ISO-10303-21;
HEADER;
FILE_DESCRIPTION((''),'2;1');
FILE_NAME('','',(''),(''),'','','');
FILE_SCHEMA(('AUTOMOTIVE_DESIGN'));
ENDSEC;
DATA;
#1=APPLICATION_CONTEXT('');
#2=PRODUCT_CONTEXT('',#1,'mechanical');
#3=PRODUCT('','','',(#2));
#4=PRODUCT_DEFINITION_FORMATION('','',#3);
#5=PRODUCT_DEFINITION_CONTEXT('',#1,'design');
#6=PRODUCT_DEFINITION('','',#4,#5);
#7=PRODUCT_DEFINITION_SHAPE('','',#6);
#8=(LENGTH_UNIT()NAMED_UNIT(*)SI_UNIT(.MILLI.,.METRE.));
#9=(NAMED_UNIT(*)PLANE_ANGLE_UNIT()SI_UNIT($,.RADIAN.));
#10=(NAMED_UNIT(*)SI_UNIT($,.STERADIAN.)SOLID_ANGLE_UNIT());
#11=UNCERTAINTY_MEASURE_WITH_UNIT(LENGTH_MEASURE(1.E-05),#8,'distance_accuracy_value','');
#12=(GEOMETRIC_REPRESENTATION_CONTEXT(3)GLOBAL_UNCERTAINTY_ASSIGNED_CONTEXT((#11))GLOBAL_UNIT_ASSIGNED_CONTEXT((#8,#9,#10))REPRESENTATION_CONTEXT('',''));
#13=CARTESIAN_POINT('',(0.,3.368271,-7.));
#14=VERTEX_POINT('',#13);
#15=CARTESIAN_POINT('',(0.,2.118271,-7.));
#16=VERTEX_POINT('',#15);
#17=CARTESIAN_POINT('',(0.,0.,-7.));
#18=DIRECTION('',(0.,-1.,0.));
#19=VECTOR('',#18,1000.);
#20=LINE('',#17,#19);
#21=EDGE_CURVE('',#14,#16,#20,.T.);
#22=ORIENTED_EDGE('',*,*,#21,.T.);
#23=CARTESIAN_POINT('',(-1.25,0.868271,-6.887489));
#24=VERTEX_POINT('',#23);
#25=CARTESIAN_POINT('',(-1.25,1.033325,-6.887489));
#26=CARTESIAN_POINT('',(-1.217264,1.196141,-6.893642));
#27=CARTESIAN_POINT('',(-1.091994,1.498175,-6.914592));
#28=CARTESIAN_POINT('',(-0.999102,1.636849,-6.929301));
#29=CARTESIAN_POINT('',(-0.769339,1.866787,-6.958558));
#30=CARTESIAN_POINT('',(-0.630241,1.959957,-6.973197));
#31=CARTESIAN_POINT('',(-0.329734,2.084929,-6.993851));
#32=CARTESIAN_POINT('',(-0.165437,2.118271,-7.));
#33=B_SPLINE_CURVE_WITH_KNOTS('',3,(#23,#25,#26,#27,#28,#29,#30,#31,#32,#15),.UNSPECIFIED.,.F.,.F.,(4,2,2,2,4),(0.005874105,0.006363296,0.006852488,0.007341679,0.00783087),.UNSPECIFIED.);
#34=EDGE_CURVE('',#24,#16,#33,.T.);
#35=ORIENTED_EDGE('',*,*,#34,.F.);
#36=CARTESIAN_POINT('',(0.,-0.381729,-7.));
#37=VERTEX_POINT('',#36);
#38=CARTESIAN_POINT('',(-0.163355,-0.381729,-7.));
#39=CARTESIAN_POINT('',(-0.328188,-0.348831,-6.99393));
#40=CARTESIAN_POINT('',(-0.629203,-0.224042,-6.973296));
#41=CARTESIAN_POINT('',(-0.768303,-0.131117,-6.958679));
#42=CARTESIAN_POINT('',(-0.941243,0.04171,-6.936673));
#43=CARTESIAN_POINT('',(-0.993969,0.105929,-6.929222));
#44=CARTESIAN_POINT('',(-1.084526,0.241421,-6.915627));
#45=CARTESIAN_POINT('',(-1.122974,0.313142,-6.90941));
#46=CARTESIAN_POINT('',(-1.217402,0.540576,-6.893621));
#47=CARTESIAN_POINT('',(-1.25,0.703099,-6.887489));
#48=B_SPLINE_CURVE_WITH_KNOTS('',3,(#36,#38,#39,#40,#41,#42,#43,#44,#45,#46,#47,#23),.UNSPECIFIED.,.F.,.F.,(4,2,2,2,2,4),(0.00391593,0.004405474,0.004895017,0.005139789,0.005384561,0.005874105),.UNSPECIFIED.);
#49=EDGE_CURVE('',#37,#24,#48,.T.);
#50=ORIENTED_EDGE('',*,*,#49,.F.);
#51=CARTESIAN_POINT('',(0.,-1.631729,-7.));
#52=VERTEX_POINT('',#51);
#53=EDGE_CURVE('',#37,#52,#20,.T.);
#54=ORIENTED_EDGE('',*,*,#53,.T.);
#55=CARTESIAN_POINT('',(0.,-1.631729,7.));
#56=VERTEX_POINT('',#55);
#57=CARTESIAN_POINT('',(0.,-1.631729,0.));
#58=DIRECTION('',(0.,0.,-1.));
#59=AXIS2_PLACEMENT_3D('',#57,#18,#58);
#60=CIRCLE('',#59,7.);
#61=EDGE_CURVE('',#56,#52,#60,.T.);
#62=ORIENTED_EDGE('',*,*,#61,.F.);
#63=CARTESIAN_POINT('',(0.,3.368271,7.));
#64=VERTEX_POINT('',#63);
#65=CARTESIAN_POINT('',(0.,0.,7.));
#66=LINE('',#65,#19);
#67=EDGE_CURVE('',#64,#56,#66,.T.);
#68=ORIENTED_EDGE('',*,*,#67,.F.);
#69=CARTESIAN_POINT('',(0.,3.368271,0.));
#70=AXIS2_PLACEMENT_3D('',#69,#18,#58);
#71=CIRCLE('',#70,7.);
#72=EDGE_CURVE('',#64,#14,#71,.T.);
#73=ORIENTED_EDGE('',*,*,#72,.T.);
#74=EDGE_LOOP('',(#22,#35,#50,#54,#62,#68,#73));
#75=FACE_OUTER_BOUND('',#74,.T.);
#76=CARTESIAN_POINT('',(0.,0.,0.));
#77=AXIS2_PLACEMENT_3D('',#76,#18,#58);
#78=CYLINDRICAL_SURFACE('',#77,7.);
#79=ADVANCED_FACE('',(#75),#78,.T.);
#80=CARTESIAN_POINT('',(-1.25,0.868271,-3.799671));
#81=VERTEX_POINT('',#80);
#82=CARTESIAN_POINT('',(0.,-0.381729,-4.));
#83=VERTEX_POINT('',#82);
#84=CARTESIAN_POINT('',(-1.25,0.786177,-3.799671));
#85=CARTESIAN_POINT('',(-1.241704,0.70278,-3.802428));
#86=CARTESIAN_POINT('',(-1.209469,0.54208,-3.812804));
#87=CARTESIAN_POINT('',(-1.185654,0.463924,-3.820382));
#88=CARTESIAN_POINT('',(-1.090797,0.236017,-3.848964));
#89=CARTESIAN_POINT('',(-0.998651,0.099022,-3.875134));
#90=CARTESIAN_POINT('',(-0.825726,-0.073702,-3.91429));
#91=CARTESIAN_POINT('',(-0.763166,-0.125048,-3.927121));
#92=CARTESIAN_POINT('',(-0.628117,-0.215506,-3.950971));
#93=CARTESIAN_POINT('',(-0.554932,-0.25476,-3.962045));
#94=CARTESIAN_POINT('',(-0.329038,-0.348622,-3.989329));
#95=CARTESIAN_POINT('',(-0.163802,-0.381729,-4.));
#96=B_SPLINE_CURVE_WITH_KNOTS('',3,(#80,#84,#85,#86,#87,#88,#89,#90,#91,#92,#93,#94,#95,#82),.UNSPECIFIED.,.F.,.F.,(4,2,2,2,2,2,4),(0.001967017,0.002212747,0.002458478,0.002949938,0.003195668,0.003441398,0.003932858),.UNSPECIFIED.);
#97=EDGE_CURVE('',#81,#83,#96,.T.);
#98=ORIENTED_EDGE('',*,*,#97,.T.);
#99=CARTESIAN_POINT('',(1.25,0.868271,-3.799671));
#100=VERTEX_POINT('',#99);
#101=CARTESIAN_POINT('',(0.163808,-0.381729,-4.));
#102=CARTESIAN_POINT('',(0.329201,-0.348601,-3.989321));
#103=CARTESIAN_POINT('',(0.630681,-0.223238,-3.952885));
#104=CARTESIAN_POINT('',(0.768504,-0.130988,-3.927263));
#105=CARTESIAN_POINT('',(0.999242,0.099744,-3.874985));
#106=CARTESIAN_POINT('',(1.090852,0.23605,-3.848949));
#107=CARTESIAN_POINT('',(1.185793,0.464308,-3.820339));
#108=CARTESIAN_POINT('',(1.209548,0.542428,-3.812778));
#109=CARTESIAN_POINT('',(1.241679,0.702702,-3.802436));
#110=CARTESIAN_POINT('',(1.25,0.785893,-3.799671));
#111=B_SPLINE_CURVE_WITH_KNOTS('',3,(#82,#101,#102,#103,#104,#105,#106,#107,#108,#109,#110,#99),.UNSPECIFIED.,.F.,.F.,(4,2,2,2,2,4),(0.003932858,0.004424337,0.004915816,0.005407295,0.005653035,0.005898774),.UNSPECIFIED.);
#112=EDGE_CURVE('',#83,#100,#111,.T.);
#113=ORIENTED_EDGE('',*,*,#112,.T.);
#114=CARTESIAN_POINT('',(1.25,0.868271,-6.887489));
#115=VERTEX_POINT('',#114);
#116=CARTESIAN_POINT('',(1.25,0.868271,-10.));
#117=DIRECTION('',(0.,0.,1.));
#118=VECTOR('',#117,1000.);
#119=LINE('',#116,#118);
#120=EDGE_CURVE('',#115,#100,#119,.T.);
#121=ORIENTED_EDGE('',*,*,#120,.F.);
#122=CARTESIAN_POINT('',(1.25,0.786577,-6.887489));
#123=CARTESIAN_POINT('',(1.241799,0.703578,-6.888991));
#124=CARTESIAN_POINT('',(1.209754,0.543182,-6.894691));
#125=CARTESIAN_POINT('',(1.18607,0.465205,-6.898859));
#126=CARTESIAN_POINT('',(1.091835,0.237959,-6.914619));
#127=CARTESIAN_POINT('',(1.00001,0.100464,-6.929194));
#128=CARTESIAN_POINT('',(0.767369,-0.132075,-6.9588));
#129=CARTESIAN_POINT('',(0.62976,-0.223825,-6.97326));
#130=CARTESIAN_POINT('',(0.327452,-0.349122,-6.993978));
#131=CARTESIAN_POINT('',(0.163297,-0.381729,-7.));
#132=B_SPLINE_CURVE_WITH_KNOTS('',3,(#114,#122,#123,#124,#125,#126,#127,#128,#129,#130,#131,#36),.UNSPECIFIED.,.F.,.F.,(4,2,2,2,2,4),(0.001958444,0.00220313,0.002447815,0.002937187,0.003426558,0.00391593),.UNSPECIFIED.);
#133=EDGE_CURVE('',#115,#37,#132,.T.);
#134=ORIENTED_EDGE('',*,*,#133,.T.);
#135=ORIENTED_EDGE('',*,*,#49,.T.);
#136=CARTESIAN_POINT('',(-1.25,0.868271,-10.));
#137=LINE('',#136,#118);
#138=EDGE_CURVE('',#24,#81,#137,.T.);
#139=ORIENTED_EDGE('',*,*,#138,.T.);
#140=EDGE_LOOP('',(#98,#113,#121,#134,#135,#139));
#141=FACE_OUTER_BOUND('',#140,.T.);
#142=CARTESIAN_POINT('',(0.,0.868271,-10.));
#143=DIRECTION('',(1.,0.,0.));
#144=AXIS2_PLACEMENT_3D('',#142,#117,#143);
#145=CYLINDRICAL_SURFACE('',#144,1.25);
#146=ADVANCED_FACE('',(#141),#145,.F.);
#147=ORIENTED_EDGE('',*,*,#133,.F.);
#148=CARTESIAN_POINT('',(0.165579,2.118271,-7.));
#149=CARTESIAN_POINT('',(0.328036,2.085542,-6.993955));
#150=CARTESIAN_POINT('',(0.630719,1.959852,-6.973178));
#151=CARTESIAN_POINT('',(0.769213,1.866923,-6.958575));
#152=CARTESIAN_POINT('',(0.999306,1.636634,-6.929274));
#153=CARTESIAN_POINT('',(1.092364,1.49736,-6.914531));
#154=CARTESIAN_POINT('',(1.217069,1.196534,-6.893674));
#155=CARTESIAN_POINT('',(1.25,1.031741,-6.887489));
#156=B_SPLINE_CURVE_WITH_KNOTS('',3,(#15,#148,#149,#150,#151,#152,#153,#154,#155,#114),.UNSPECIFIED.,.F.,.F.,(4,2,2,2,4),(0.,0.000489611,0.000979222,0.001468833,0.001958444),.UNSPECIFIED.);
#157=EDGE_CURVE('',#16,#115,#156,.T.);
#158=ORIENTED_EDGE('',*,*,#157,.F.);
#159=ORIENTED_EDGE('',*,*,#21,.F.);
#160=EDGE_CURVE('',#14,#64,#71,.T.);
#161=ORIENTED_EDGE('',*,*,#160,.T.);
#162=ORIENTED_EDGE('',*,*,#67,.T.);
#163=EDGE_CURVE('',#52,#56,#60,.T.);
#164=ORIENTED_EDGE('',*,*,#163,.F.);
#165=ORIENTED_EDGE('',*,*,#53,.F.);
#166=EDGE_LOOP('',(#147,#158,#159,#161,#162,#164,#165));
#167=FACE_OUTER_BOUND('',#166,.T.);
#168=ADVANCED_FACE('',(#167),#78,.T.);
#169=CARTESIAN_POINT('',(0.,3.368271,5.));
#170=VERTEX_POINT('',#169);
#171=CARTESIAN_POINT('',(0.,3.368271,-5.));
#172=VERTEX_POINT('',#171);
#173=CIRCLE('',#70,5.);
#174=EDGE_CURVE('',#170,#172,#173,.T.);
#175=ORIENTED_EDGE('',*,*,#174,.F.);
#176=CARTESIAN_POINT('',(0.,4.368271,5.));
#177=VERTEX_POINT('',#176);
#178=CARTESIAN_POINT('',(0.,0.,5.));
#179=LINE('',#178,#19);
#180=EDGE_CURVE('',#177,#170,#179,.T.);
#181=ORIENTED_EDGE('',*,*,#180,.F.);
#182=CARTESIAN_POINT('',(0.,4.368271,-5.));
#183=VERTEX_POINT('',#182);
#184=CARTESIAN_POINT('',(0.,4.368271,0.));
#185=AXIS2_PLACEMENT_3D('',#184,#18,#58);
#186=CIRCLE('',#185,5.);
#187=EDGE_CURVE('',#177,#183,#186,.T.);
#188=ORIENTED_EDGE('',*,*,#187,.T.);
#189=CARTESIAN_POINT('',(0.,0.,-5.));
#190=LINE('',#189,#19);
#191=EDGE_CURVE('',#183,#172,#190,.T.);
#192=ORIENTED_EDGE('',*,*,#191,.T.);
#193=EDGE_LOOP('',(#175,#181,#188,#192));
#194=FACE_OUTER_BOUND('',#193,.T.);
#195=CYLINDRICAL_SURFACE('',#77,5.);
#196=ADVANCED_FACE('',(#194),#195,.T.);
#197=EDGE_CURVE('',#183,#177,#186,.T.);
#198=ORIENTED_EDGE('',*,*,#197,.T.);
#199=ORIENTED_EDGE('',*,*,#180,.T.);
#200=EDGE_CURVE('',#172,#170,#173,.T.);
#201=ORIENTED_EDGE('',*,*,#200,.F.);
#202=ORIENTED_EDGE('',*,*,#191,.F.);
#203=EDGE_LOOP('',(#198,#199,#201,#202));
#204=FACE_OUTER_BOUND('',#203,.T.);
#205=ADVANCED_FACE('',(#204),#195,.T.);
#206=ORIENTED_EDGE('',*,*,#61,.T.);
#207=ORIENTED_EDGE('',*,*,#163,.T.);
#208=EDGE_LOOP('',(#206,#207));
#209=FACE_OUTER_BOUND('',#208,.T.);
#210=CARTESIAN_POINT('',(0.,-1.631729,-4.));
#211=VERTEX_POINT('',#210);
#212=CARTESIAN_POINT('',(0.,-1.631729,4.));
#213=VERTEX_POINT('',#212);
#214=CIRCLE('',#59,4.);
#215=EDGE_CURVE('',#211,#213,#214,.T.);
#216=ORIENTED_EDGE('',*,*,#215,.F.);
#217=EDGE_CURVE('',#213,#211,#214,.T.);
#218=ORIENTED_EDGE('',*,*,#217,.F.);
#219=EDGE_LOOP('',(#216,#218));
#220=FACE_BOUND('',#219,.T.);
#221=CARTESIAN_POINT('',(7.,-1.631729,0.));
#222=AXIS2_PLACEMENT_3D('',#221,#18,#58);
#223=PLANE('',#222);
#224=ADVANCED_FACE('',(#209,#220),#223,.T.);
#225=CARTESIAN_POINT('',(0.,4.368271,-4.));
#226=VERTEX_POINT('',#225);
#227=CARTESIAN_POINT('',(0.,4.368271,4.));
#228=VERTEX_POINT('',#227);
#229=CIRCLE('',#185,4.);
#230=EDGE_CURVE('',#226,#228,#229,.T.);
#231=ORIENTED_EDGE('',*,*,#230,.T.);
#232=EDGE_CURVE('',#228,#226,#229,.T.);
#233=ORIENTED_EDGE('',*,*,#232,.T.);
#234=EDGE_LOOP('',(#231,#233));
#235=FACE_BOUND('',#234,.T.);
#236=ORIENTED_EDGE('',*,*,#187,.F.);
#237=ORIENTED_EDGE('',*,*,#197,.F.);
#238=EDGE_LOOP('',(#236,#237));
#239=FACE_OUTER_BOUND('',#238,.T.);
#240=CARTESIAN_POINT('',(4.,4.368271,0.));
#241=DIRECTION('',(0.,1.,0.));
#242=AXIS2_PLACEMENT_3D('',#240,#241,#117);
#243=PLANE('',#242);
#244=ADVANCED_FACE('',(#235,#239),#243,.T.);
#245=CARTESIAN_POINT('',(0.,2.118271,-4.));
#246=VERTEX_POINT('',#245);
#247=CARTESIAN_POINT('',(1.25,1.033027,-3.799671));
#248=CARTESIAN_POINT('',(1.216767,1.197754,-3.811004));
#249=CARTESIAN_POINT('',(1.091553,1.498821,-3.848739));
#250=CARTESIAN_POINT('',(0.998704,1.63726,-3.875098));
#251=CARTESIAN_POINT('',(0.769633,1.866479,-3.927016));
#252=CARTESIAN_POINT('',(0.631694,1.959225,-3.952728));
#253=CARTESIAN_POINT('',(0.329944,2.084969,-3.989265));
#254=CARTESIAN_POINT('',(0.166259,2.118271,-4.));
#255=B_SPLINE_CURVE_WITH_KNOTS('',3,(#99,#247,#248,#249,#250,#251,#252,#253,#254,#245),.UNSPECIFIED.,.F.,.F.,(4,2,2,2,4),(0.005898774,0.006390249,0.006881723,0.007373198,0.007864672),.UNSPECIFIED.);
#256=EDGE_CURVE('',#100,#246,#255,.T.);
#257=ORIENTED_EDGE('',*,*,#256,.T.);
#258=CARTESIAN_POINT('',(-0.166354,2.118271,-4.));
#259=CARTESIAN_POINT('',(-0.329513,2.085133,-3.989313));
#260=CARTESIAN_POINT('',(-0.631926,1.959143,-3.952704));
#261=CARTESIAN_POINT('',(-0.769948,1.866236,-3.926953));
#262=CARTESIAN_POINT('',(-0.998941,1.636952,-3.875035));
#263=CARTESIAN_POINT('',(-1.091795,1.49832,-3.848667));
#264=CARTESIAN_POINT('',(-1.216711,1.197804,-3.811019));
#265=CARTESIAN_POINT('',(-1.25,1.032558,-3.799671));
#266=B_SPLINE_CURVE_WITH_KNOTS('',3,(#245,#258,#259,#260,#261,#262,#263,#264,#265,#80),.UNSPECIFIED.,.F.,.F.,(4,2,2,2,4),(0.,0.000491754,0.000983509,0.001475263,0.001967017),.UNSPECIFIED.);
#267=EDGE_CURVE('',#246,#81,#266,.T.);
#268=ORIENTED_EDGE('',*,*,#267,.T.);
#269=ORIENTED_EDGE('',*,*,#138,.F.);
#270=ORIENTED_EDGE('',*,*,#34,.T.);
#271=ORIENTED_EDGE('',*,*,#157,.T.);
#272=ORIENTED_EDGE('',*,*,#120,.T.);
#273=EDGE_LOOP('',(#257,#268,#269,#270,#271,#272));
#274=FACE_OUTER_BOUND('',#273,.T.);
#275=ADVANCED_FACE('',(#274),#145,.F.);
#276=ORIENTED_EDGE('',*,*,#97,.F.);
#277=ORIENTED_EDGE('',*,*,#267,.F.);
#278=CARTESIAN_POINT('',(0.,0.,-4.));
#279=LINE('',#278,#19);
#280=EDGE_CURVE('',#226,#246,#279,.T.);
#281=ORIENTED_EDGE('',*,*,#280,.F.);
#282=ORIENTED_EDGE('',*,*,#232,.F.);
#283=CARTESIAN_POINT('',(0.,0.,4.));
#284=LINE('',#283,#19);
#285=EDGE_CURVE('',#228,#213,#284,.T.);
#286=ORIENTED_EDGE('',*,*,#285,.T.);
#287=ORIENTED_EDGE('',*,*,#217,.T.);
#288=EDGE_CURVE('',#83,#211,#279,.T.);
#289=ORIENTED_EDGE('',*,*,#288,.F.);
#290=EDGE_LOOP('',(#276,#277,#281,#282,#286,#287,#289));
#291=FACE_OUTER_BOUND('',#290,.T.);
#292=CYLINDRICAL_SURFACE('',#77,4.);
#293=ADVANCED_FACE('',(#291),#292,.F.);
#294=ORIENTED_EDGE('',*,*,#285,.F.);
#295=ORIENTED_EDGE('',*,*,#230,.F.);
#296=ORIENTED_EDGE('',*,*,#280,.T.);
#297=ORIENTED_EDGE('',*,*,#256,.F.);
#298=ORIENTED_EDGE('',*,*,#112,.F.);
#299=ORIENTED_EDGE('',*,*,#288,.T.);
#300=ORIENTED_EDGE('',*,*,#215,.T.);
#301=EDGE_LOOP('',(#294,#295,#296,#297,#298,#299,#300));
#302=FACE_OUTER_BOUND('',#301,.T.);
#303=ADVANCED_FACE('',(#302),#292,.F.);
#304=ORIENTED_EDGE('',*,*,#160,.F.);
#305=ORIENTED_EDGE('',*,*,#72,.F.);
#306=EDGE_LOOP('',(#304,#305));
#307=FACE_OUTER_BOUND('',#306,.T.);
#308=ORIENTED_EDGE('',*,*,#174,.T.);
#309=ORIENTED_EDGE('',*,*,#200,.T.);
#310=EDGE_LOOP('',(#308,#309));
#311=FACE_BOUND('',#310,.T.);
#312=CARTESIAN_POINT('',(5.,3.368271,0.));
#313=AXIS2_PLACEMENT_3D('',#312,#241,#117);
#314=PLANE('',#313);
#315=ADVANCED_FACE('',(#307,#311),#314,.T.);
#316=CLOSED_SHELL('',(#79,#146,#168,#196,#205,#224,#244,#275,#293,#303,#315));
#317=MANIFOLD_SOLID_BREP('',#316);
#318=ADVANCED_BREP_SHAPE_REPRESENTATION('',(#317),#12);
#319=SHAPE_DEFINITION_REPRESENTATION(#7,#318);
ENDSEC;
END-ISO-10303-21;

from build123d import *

# Parameters (mm, degrees)
SKETCH_2_R          = 1.25
CUT_EXTRUDE_1_DEPTH = 10


with BuildPart() as part:
    # 草图1 → 旋转1 (revolve)
    with BuildSketch(Plane.XY, mode=Mode.PRIVATE) as revolve_1_sk:
        Polygon((4, 4.368271468), (5, 4.368271468), (5, 3.368271468), (7, 3.368271468), (7, -1.631728532), (4, -1.631728532), align=None)
    revolve(revolve_1_sk.sketch.rotate(Axis((0, 0, 0), (0, 1, 0)), 90), axis=Axis((0, 0, 0), (0, 1, 0)))

    # 草图2 → 切除-拉伸1 (cut)
    with BuildSketch(Plane.XY):
        with Locations(Location((0, 0.868271468, 0), (0, 0, 270.000000001))):
            Circle(SKETCH_2_R)
    extrude(amount=-CUT_EXTRUDE_1_DEPTH, mode=Mode.SUBTRACT)


solid = part.part
